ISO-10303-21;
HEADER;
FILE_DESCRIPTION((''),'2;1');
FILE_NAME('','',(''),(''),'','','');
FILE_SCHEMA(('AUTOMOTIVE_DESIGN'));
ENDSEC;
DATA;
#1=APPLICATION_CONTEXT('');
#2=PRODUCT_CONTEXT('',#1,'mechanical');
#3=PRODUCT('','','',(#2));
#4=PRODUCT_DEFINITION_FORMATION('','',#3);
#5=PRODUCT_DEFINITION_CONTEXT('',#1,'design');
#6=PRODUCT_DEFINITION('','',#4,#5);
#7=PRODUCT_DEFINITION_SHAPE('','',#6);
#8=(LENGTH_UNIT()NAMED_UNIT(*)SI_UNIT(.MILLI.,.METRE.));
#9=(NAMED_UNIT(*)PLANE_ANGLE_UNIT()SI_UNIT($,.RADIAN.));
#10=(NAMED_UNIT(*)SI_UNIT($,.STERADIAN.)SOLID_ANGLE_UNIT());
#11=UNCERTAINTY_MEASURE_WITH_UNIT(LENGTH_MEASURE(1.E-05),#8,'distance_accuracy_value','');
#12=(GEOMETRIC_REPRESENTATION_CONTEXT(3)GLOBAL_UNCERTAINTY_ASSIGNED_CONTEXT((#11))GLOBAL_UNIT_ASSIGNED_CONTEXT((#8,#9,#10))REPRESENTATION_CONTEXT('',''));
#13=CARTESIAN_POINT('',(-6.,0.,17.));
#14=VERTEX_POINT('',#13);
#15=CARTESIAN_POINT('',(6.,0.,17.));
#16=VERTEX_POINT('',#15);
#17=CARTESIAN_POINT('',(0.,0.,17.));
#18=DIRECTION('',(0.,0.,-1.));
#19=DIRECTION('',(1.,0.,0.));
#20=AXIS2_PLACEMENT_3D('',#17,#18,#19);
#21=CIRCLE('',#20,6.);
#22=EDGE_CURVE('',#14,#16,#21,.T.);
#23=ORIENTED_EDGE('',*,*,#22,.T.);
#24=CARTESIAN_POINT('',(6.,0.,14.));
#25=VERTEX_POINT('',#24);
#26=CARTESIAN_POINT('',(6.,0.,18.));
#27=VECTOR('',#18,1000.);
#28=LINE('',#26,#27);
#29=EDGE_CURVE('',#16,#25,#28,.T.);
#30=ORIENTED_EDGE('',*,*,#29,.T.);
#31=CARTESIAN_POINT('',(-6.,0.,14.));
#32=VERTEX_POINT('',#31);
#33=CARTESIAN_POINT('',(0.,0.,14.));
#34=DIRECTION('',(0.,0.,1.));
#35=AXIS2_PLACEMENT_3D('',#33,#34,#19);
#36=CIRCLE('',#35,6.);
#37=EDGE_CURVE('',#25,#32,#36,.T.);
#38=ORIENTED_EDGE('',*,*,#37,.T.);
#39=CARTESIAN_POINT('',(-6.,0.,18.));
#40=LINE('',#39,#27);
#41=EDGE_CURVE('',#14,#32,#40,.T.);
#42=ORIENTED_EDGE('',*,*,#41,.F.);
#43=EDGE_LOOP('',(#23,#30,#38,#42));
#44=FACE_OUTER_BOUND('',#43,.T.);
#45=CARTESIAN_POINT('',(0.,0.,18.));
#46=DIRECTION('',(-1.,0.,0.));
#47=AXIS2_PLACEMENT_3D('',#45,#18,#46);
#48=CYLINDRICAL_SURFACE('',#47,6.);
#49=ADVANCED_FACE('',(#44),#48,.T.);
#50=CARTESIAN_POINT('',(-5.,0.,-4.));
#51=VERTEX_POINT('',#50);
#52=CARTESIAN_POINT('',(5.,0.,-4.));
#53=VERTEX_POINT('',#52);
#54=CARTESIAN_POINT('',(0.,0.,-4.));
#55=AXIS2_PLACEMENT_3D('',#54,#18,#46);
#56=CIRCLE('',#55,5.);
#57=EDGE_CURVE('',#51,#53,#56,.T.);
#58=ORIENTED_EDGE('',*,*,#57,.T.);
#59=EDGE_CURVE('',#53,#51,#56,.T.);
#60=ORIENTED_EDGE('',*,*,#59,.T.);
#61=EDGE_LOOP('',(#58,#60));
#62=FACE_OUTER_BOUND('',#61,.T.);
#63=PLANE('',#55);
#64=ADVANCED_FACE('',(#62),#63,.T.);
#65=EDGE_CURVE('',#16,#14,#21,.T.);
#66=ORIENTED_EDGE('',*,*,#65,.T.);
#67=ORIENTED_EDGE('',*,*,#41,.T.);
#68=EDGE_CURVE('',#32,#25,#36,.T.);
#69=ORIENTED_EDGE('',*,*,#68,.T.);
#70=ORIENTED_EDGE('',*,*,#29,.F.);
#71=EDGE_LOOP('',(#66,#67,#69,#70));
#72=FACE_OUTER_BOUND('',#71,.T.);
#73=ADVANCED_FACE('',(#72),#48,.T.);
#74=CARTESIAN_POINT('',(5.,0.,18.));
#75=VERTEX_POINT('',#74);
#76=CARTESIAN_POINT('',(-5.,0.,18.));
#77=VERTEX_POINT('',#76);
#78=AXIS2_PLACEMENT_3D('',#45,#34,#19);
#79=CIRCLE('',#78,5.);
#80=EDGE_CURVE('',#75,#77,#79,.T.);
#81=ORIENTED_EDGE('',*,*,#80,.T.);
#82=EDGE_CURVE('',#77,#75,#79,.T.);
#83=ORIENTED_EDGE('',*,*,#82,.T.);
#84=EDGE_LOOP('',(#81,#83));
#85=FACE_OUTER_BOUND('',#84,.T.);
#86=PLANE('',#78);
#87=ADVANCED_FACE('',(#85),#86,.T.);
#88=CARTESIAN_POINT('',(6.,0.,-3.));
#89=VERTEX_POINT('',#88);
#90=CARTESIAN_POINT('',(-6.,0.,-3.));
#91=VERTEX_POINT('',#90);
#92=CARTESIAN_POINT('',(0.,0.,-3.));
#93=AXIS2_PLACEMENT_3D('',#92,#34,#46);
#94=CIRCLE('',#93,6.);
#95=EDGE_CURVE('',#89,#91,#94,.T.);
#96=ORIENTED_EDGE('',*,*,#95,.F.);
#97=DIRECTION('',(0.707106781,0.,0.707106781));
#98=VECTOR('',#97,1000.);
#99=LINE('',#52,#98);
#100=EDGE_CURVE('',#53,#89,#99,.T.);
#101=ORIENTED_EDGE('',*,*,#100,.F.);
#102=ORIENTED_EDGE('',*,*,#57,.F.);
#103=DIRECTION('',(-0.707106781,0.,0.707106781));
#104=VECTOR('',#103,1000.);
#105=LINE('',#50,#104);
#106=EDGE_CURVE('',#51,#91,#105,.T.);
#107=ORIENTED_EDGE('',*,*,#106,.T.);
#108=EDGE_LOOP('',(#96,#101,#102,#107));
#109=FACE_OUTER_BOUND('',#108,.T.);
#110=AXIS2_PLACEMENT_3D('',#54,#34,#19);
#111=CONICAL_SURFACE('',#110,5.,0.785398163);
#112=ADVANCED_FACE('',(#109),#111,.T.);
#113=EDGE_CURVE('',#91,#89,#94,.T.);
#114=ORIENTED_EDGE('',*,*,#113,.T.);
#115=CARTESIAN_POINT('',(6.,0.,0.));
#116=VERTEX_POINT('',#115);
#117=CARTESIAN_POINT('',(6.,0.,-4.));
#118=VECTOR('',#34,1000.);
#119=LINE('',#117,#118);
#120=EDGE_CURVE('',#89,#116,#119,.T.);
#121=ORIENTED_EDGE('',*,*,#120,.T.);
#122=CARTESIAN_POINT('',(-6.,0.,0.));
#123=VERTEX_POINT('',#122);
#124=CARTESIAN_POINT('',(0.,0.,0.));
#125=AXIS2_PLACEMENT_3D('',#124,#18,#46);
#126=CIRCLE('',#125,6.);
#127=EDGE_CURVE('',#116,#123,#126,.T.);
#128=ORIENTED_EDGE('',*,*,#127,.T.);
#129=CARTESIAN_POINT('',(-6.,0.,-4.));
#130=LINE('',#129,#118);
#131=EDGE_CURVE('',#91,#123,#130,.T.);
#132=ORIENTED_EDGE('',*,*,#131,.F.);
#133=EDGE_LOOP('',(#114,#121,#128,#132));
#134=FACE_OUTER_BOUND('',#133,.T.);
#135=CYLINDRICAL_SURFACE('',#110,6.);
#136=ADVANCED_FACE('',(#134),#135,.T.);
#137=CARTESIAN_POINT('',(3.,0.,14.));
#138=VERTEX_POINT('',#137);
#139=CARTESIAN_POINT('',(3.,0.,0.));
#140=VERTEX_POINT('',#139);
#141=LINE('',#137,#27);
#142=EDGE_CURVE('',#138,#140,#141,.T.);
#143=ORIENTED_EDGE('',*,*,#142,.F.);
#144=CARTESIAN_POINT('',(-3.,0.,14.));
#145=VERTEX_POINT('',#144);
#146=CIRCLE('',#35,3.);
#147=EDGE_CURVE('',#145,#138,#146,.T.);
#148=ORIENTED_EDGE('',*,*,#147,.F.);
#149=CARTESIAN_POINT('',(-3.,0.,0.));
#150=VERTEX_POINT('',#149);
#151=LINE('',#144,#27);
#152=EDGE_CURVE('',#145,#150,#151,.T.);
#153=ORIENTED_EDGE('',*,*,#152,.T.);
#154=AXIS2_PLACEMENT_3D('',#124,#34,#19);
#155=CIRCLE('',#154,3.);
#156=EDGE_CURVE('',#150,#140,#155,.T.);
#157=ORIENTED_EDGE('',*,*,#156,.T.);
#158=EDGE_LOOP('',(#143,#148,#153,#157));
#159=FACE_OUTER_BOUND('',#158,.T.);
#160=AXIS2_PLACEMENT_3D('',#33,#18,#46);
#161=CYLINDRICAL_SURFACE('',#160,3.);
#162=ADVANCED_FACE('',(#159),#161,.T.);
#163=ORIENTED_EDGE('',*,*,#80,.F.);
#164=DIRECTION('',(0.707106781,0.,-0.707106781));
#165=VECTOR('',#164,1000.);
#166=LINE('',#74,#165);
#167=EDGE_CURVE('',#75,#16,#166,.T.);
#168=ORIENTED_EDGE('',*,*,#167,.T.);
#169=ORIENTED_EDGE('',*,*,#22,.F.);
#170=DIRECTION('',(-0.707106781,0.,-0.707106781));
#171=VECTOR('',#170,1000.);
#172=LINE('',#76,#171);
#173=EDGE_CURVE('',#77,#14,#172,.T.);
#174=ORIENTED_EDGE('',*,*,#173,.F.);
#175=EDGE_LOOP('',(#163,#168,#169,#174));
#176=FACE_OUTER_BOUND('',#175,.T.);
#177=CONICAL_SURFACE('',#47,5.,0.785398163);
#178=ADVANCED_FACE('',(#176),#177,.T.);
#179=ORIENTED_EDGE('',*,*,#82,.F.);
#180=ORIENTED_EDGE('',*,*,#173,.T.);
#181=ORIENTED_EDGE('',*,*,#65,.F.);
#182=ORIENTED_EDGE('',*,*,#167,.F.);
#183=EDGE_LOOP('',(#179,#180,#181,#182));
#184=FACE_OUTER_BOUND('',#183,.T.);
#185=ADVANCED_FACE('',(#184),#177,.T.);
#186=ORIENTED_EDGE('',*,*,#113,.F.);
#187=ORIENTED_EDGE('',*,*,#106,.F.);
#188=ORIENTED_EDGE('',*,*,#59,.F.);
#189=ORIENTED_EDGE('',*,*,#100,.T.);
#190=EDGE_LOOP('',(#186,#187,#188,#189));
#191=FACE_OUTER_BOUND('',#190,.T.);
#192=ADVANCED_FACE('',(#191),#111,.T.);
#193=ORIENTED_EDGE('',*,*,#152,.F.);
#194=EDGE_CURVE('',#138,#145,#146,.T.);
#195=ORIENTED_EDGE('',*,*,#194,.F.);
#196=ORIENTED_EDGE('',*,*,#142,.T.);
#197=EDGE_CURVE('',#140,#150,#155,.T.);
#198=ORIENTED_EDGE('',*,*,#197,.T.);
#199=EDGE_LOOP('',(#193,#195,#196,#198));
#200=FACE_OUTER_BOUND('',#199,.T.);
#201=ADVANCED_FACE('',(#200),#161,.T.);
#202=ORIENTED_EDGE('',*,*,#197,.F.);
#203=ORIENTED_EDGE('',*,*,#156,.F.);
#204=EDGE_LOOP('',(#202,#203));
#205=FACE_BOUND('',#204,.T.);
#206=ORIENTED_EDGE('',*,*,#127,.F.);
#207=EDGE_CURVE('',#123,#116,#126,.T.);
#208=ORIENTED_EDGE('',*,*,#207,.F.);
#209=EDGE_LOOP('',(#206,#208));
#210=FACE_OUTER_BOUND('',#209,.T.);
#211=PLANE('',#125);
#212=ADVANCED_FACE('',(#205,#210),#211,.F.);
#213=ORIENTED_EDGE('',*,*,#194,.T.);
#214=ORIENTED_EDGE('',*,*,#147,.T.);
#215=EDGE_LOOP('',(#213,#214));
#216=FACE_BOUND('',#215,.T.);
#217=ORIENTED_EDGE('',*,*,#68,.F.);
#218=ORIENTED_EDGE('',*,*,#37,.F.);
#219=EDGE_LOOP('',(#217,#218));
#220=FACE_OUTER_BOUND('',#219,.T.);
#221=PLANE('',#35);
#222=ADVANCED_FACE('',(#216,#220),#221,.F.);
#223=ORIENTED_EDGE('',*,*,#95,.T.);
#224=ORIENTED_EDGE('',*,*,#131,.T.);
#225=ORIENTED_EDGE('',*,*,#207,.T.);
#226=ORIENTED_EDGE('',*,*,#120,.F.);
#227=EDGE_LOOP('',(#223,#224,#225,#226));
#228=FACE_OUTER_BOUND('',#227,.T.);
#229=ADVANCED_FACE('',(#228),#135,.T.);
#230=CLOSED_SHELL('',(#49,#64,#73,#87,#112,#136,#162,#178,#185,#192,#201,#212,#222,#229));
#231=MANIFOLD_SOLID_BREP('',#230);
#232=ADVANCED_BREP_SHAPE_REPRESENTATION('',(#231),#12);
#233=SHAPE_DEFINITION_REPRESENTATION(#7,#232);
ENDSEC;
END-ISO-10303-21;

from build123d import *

# Parameters (mm, degrees)
SKETCH_1_R      = 3
EXTRUDE_1_DEPTH = 14
SKETCH_2_R      = 6
EXTRUDE_2_DEPTH = 4
CHAMFER_1_SIZE  = 1
EXTRUDE_START   = 4
SKETCH_3_R      = 6
EXTRUDE_3_DEPTH = 4
CHAMFER_2_SIZE  = 1


with BuildPart() as part:
    # 草图1 → 凸台-拉伸1 (new body)
    with BuildSketch(Plane.XY):
        Circle(SKETCH_1_R)
    extrude(amount=EXTRUDE_1_DEPTH)

    # 草图2 → 凸台-拉伸2 (add)
    with BuildSketch(Plane.XY.offset(14)):
        Circle(SKETCH_2_R)
    extrude(amount=EXTRUDE_2_DEPTH)

    # 倒角1
    chamfer_1_edges = [part.edges().sort_by_distance(p)[0] for p in [
        (-6, 0, 18),
    ]]
    chamfer(chamfer_1_edges, length=CHAMFER_1_SIZE)

    # 草图3 → 凸台-拉伸3 (add)
    with BuildSketch(Plane(origin=(0, 0, 0), x_dir=(-1, 0, 0), z_dir=(0, 0, -1)).offset(EXTRUDE_START)):
        with Locations(Location((0, 0, 0), (0, 0, 180))):
            Circle(SKETCH_3_R)
    extrude(amount=-EXTRUDE_3_DEPTH)

    # 倒角2
    chamfer_2_edges = [part.edges().sort_by_distance(p)[0] for p in [
        (-6, 0, -4),
    ]]
    chamfer(chamfer_2_edges, length=CHAMFER_2_SIZE)


solid = part.part
